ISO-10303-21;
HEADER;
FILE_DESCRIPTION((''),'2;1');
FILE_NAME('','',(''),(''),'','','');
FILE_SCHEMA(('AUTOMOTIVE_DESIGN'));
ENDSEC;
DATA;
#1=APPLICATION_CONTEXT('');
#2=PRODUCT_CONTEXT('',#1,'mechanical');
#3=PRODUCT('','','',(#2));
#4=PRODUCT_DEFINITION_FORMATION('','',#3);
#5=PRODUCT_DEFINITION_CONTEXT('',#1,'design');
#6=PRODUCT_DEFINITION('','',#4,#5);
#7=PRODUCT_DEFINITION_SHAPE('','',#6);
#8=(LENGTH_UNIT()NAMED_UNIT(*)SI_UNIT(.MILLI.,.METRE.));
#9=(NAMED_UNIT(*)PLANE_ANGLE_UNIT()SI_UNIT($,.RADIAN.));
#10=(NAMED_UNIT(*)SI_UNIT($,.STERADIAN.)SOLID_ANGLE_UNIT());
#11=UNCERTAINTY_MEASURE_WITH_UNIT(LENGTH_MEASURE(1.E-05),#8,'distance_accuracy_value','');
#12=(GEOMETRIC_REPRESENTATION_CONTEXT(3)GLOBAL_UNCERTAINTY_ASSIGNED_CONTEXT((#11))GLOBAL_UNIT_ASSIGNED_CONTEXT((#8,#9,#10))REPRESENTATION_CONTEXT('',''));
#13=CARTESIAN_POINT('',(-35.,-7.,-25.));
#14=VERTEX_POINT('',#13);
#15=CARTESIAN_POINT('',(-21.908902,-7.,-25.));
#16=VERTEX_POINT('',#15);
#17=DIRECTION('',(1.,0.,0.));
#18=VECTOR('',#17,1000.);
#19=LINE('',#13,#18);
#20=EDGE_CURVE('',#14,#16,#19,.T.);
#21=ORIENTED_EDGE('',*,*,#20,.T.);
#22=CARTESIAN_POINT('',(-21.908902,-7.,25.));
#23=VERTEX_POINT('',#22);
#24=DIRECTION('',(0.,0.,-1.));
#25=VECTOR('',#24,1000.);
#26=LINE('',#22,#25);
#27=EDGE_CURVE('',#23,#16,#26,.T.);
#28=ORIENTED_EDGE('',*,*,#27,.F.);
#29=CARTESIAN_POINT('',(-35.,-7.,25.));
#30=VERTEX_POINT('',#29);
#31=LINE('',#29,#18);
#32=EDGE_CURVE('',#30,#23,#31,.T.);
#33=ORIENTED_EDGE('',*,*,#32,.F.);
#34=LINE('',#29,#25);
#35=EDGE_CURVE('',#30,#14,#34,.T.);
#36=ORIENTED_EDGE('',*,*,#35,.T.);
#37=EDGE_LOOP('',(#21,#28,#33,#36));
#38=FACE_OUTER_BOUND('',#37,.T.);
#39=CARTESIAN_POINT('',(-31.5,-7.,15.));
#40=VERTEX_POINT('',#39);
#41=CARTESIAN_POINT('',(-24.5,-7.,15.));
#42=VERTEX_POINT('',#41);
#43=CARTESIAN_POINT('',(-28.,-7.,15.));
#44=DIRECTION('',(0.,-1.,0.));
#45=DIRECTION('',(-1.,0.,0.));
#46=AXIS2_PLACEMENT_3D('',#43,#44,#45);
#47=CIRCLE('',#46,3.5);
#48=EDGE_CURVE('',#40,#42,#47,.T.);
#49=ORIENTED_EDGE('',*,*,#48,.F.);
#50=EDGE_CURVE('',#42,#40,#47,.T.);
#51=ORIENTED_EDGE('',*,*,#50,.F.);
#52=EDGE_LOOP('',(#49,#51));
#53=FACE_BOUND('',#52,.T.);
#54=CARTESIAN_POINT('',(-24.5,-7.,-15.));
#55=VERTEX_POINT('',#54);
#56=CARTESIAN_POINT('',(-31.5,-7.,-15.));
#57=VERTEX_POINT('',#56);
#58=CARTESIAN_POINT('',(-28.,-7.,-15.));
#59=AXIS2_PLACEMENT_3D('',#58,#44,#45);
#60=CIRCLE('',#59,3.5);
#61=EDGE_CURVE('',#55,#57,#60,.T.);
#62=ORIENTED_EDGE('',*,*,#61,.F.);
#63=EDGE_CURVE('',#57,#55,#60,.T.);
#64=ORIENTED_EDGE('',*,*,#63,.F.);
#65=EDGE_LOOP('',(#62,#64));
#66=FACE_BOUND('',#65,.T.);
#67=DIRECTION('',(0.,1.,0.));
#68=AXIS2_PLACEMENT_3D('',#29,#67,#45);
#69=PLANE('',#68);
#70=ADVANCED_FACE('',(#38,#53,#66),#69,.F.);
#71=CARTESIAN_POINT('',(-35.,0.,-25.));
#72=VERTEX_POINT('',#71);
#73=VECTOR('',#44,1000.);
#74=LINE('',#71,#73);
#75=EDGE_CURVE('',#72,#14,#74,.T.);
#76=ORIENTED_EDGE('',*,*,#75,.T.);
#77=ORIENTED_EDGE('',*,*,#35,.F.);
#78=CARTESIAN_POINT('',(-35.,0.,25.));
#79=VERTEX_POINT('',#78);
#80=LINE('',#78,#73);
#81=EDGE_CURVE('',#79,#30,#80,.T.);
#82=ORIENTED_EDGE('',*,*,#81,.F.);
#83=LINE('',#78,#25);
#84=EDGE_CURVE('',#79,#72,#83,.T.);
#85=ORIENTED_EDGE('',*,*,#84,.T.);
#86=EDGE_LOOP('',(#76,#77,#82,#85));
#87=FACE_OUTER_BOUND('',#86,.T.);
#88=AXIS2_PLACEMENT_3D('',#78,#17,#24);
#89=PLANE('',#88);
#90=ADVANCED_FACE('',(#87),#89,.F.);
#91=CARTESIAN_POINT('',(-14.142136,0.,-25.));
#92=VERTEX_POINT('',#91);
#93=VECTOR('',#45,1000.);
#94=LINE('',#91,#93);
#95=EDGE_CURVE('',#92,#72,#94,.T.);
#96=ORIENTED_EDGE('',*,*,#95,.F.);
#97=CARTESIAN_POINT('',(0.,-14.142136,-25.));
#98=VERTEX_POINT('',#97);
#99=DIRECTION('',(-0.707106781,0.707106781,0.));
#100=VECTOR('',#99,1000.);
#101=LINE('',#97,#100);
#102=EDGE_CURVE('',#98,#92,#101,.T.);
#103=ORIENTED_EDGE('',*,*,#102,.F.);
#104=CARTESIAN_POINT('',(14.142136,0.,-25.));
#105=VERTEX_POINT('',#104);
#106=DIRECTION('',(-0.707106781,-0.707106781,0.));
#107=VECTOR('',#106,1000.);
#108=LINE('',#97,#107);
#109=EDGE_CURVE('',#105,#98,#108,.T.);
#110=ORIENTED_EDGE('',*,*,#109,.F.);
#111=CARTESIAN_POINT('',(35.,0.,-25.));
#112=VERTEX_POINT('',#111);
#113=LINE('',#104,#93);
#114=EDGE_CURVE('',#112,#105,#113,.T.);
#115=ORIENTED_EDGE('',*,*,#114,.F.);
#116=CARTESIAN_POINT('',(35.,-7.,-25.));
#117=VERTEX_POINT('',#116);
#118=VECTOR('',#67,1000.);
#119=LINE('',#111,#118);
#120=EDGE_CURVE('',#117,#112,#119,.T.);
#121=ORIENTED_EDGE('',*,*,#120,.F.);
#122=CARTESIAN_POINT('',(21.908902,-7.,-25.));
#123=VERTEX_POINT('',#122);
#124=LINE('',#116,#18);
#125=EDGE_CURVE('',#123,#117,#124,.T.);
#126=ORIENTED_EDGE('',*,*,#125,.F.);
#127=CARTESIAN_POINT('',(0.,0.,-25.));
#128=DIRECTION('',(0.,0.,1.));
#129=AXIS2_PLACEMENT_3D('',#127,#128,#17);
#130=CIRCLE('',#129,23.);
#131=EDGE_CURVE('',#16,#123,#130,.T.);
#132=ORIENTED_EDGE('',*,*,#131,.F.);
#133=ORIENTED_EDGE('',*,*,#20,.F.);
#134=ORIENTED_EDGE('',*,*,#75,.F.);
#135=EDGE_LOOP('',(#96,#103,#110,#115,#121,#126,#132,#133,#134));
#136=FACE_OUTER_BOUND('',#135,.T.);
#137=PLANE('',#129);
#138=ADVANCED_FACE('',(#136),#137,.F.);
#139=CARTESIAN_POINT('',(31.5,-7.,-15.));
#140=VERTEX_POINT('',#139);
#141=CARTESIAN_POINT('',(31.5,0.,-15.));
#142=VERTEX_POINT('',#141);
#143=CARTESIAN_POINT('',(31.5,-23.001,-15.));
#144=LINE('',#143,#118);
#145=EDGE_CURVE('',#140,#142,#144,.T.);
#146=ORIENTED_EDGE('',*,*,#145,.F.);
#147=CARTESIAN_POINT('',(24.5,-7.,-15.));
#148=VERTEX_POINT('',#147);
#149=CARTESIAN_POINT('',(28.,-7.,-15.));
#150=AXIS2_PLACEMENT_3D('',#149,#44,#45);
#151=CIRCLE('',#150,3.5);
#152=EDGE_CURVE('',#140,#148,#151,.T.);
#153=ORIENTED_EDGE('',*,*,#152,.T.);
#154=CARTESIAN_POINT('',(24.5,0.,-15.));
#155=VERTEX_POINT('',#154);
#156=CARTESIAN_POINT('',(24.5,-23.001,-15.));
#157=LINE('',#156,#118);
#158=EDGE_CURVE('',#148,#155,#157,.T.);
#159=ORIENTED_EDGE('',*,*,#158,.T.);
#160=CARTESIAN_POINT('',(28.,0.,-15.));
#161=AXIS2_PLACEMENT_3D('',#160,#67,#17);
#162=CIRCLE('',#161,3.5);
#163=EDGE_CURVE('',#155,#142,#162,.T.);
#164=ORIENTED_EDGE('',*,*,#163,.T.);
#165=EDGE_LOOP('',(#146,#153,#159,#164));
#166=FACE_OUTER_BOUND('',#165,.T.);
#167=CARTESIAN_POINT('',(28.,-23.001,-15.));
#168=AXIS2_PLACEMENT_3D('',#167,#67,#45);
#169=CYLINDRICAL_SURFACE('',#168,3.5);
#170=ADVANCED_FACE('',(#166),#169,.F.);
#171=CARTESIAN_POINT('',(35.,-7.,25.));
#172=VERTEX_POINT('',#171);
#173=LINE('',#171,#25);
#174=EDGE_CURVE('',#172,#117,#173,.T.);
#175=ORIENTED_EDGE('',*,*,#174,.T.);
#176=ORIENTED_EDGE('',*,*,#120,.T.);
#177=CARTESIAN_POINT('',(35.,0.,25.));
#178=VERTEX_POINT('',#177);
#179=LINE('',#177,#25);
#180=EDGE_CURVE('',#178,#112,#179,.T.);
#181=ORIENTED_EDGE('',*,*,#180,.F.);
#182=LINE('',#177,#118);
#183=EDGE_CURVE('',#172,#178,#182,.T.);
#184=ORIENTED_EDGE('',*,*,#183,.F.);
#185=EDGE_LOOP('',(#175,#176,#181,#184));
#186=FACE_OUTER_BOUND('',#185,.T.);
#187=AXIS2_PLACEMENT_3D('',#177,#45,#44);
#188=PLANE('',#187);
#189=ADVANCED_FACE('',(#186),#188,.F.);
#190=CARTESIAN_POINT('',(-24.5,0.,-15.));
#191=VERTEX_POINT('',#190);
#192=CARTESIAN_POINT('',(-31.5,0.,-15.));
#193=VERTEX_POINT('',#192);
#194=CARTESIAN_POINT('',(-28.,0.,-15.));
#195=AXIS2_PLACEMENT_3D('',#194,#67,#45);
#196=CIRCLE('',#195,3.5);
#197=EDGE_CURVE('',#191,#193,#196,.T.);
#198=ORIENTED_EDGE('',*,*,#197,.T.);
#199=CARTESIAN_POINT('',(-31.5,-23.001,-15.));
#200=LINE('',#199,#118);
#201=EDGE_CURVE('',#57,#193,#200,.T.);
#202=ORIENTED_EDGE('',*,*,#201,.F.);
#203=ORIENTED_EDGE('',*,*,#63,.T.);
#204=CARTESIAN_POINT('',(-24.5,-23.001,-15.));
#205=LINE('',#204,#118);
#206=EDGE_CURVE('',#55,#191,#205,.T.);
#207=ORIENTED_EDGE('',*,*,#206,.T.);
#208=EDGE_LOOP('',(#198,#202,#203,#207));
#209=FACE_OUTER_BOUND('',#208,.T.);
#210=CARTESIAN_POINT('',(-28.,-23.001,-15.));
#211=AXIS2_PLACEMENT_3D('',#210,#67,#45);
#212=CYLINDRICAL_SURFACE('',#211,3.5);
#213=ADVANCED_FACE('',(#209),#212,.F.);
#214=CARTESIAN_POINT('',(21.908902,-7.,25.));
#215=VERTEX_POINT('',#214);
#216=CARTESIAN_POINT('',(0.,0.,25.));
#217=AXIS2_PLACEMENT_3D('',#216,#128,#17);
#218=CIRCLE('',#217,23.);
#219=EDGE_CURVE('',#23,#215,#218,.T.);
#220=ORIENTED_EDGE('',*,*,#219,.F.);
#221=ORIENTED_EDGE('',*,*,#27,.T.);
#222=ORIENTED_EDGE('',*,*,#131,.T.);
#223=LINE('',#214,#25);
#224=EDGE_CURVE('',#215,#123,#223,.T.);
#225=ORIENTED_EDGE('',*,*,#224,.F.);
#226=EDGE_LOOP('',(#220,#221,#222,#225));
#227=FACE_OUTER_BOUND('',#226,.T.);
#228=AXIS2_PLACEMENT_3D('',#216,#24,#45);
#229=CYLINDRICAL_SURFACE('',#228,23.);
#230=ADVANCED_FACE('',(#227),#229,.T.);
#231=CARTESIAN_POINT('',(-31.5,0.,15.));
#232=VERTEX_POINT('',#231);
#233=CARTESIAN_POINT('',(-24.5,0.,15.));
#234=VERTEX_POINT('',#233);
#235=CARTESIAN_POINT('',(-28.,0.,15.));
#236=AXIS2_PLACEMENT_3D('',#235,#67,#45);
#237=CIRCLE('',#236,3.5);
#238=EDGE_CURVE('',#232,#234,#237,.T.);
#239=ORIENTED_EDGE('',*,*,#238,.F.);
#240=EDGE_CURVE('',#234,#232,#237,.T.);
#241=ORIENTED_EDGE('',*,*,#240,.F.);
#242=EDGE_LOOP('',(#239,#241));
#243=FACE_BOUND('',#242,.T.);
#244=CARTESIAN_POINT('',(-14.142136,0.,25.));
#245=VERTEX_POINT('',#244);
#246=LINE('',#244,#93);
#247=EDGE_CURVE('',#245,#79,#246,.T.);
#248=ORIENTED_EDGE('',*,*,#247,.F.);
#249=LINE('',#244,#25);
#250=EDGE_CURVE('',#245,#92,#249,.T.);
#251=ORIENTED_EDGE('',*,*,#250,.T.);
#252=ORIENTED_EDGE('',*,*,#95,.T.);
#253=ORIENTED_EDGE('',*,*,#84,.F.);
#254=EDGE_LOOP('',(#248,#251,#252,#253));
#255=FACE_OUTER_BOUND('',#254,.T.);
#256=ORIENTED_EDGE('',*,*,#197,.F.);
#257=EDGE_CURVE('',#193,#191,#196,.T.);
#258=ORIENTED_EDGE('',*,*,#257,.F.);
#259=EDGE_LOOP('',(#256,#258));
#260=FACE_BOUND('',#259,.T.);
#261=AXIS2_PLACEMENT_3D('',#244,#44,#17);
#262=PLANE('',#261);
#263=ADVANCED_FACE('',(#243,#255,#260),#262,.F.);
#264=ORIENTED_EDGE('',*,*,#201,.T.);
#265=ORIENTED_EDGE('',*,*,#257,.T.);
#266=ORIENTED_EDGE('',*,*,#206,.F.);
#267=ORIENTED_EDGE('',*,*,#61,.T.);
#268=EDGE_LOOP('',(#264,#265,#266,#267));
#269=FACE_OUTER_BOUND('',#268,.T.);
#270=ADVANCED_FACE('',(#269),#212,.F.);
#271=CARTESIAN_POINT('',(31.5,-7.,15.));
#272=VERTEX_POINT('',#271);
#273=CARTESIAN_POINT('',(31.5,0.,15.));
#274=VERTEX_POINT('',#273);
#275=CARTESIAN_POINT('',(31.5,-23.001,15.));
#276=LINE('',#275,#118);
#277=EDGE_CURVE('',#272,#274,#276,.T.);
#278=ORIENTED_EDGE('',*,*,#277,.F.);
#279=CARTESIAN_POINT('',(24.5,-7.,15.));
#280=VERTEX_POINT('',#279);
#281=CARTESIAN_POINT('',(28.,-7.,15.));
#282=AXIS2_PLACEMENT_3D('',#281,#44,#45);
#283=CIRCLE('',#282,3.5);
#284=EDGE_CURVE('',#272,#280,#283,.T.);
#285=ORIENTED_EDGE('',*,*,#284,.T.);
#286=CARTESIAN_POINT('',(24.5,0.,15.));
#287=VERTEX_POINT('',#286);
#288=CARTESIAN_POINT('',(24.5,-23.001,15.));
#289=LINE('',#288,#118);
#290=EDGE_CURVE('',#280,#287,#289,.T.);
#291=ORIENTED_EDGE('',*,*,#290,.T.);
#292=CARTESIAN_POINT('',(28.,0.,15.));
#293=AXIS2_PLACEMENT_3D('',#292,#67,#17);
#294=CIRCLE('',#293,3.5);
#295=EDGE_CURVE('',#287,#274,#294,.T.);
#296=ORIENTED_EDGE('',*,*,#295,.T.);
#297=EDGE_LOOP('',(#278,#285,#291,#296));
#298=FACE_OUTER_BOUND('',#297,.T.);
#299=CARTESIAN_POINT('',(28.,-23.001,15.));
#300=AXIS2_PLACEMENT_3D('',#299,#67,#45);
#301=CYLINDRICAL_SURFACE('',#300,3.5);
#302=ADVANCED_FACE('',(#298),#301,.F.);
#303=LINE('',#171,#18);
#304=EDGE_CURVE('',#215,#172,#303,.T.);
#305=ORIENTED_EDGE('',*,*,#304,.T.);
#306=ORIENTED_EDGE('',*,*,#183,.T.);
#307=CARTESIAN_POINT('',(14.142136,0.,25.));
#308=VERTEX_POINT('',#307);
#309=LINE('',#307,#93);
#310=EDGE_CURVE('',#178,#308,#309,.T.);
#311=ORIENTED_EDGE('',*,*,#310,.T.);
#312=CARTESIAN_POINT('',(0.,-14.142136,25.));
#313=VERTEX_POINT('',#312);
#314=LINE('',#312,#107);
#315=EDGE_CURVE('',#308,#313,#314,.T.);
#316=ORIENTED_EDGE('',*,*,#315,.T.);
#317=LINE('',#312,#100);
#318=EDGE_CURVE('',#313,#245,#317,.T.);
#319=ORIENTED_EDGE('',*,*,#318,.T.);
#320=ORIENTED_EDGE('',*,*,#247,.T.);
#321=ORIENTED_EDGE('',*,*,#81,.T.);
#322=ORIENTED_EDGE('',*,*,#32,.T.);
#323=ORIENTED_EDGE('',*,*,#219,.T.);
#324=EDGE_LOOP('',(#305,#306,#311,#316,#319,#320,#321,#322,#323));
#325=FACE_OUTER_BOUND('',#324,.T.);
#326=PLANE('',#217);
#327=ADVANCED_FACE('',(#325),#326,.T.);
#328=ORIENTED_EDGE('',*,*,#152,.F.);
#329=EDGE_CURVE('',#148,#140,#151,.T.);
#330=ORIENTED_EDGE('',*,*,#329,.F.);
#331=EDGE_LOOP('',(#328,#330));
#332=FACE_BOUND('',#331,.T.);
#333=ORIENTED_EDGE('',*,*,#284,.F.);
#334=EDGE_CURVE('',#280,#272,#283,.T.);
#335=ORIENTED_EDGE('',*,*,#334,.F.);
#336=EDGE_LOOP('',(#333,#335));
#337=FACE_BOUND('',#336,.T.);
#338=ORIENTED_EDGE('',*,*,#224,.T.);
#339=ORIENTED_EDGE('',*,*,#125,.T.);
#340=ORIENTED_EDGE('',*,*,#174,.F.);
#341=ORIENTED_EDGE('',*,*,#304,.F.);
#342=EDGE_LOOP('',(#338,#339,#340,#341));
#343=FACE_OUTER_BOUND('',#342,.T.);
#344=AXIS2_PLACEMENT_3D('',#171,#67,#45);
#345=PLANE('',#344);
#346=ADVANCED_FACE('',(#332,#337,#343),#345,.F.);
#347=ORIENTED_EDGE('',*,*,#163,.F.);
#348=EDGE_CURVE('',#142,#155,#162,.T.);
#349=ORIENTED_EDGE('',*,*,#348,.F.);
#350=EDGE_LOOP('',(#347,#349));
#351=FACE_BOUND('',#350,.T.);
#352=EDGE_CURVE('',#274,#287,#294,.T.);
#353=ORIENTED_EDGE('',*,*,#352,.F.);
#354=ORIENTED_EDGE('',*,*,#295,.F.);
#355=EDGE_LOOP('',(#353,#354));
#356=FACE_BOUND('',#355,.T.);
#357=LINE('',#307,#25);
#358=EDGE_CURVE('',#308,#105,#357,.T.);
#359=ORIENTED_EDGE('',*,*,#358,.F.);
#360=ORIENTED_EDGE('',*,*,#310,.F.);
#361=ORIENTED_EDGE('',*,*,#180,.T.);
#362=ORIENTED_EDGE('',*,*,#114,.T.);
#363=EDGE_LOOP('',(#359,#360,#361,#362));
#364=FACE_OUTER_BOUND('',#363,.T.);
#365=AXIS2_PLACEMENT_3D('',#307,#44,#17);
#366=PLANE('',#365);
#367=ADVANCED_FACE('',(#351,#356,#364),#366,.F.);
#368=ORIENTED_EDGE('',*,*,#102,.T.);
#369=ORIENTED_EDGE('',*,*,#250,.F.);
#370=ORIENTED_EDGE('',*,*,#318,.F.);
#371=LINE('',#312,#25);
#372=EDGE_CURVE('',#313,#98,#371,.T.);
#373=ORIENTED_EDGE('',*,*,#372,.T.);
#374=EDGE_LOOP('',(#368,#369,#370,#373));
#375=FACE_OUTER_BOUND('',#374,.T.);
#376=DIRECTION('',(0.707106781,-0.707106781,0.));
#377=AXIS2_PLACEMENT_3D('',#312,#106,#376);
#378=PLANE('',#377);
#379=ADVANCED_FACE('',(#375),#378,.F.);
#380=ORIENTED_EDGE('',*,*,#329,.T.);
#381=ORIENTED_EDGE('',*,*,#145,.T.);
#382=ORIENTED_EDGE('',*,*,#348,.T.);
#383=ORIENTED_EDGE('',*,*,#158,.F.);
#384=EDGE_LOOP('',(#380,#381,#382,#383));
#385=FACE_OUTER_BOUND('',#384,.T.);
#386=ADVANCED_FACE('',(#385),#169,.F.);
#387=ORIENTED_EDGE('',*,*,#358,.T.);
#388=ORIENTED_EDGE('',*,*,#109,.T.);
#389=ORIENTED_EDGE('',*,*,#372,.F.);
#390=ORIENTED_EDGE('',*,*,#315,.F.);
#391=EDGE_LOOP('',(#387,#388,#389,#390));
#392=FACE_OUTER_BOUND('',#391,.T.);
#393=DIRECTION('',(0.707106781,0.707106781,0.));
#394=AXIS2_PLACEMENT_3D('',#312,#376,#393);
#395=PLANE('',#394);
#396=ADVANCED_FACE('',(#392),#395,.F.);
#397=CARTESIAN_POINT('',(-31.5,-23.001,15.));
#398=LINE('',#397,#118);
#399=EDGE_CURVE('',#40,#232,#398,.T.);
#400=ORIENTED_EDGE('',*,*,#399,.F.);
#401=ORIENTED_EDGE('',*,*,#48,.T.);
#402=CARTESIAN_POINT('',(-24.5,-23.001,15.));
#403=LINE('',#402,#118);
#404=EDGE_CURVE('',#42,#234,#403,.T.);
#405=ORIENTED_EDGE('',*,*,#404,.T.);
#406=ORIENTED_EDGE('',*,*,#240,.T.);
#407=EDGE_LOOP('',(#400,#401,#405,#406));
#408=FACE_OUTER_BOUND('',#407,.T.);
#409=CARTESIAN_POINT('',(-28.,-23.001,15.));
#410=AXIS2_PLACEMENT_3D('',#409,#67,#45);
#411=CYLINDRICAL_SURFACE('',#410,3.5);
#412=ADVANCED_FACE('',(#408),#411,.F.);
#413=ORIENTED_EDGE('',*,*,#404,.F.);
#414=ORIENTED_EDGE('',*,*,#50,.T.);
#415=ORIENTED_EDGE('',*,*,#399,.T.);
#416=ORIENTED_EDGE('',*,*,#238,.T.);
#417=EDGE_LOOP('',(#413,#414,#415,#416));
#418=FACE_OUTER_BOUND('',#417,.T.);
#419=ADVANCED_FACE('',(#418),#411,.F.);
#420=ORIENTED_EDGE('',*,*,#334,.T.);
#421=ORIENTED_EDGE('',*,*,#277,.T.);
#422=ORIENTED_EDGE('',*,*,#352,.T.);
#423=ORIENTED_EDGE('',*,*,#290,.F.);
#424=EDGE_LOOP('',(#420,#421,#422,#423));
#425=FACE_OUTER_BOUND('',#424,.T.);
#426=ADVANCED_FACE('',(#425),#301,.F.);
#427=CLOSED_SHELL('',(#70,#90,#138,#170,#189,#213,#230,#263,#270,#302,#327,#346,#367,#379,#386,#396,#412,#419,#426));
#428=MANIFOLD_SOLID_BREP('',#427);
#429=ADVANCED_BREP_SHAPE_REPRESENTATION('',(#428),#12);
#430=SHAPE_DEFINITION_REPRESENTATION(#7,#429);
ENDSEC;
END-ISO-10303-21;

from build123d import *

# Parameters (mm, degrees)
SADDLE_BODY_DEPTH           = 25
FLANGE_MOUNTING_HOLES_REACH = 50.775
FLANGE_HOLES_SKETCH_R       = 3.5


with BuildPart() as part:
    # Saddle Profile Sketch → Saddle Body (new, symmetric)
    with BuildSketch(Plane.XY):
        with BuildLine():
            Line((0, -14.142135624), (14.142135624, 0))
            Line((14.142135624, 0), (35, 0))
            Line((35, 0), (35, -7))
            Line((35, -7), (21.9089023, -7))
            ThreePointArc((21.9089023, -7), (0, -23), (-21.9089023, -7))
            Line((-21.9089023, -7), (-35, -7))
            Line((-35, -7), (-35, 0))
            Line((-35, 0), (-14.142135624, 0))
            Line((-14.142135624, 0), (0, -14.142135624))
        make_face()
    extrude(amount=SADDLE_BODY_DEPTH, both=True)

    # Flange Holes Sketch → Flange Mounting Holes (cut, up to next)
    with BuildSketch(Plane(origin=(0, 0, 0), x_dir=(1, 0, 0), z_dir=(0, 1, 0)), mode=Mode.PRIVATE) as flange_mounting_holes_sk1:
        with Locations(Location((-28, 15, 0), (0, 0, 180))):
            Circle(FLANGE_HOLES_SKETCH_R)
    flange_mounting_holes_tool1 = extrude(flange_mounting_holes_sk1.sketch, amount=-FLANGE_MOUNTING_HOLES_REACH, mode=Mode.PRIVATE) & part.part
    # Flange Holes Sketch → Flange Mounting Holes (cut, up to next)
    with BuildSketch(Plane(origin=(0, 0, 0), x_dir=(1, 0, 0), z_dir=(0, 1, 0)), mode=Mode.PRIVATE) as flange_mounting_holes_sk2:
        with Locations(Location((-28, -15, 0), (0, 0, 180))):
            Circle(FLANGE_HOLES_SKETCH_R)
    flange_mounting_holes_tool2 = extrude(flange_mounting_holes_sk2.sketch, amount=-FLANGE_MOUNTING_HOLES_REACH, mode=Mode.PRIVATE) & part.part
    # Flange Holes Sketch → Flange Mounting Holes (cut, up to next)
    with BuildSketch(Plane(origin=(0, 0, 0), x_dir=(1, 0, 0), z_dir=(0, 1, 0)), mode=Mode.PRIVATE) as flange_mounting_holes_sk3:
        with Locations(Location((28, -15, 0), (0, 0, 180))):
            Circle(FLANGE_HOLES_SKETCH_R)
    flange_mounting_holes_tool3 = extrude(flange_mounting_holes_sk3.sketch, amount=-FLANGE_MOUNTING_HOLES_REACH, mode=Mode.PRIVATE) & part.part
    # Flange Holes Sketch → Flange Mounting Holes (cut, up to next)
    with BuildSketch(Plane(origin=(0, 0, 0), x_dir=(1, 0, 0), z_dir=(0, 1, 0)), mode=Mode.PRIVATE) as flange_mounting_holes_sk4:
        with Locations(Location((28, 15, 0), (0, 0, 180))):
            Circle(FLANGE_HOLES_SKETCH_R)
    flange_mounting_holes_tool4 = extrude(flange_mounting_holes_sk4.sketch, amount=-FLANGE_MOUNTING_HOLES_REACH, mode=Mode.PRIVATE) & part.part
    add(flange_mounting_holes_tool1.solids().sort_by_distance((-28, 0, -15))[0], mode=Mode.SUBTRACT)
    add(flange_mounting_holes_tool2.solids().sort_by_distance((-28, 0, 15))[0], mode=Mode.SUBTRACT)
    add(flange_mounting_holes_tool3.solids().sort_by_distance((28, 0, 15))[0], mode=Mode.SUBTRACT)
    add(flange_mounting_holes_tool4.solids().sort_by_distance((28, 0, -15))[0], mode=Mode.SUBTRACT)


solid = part.part
